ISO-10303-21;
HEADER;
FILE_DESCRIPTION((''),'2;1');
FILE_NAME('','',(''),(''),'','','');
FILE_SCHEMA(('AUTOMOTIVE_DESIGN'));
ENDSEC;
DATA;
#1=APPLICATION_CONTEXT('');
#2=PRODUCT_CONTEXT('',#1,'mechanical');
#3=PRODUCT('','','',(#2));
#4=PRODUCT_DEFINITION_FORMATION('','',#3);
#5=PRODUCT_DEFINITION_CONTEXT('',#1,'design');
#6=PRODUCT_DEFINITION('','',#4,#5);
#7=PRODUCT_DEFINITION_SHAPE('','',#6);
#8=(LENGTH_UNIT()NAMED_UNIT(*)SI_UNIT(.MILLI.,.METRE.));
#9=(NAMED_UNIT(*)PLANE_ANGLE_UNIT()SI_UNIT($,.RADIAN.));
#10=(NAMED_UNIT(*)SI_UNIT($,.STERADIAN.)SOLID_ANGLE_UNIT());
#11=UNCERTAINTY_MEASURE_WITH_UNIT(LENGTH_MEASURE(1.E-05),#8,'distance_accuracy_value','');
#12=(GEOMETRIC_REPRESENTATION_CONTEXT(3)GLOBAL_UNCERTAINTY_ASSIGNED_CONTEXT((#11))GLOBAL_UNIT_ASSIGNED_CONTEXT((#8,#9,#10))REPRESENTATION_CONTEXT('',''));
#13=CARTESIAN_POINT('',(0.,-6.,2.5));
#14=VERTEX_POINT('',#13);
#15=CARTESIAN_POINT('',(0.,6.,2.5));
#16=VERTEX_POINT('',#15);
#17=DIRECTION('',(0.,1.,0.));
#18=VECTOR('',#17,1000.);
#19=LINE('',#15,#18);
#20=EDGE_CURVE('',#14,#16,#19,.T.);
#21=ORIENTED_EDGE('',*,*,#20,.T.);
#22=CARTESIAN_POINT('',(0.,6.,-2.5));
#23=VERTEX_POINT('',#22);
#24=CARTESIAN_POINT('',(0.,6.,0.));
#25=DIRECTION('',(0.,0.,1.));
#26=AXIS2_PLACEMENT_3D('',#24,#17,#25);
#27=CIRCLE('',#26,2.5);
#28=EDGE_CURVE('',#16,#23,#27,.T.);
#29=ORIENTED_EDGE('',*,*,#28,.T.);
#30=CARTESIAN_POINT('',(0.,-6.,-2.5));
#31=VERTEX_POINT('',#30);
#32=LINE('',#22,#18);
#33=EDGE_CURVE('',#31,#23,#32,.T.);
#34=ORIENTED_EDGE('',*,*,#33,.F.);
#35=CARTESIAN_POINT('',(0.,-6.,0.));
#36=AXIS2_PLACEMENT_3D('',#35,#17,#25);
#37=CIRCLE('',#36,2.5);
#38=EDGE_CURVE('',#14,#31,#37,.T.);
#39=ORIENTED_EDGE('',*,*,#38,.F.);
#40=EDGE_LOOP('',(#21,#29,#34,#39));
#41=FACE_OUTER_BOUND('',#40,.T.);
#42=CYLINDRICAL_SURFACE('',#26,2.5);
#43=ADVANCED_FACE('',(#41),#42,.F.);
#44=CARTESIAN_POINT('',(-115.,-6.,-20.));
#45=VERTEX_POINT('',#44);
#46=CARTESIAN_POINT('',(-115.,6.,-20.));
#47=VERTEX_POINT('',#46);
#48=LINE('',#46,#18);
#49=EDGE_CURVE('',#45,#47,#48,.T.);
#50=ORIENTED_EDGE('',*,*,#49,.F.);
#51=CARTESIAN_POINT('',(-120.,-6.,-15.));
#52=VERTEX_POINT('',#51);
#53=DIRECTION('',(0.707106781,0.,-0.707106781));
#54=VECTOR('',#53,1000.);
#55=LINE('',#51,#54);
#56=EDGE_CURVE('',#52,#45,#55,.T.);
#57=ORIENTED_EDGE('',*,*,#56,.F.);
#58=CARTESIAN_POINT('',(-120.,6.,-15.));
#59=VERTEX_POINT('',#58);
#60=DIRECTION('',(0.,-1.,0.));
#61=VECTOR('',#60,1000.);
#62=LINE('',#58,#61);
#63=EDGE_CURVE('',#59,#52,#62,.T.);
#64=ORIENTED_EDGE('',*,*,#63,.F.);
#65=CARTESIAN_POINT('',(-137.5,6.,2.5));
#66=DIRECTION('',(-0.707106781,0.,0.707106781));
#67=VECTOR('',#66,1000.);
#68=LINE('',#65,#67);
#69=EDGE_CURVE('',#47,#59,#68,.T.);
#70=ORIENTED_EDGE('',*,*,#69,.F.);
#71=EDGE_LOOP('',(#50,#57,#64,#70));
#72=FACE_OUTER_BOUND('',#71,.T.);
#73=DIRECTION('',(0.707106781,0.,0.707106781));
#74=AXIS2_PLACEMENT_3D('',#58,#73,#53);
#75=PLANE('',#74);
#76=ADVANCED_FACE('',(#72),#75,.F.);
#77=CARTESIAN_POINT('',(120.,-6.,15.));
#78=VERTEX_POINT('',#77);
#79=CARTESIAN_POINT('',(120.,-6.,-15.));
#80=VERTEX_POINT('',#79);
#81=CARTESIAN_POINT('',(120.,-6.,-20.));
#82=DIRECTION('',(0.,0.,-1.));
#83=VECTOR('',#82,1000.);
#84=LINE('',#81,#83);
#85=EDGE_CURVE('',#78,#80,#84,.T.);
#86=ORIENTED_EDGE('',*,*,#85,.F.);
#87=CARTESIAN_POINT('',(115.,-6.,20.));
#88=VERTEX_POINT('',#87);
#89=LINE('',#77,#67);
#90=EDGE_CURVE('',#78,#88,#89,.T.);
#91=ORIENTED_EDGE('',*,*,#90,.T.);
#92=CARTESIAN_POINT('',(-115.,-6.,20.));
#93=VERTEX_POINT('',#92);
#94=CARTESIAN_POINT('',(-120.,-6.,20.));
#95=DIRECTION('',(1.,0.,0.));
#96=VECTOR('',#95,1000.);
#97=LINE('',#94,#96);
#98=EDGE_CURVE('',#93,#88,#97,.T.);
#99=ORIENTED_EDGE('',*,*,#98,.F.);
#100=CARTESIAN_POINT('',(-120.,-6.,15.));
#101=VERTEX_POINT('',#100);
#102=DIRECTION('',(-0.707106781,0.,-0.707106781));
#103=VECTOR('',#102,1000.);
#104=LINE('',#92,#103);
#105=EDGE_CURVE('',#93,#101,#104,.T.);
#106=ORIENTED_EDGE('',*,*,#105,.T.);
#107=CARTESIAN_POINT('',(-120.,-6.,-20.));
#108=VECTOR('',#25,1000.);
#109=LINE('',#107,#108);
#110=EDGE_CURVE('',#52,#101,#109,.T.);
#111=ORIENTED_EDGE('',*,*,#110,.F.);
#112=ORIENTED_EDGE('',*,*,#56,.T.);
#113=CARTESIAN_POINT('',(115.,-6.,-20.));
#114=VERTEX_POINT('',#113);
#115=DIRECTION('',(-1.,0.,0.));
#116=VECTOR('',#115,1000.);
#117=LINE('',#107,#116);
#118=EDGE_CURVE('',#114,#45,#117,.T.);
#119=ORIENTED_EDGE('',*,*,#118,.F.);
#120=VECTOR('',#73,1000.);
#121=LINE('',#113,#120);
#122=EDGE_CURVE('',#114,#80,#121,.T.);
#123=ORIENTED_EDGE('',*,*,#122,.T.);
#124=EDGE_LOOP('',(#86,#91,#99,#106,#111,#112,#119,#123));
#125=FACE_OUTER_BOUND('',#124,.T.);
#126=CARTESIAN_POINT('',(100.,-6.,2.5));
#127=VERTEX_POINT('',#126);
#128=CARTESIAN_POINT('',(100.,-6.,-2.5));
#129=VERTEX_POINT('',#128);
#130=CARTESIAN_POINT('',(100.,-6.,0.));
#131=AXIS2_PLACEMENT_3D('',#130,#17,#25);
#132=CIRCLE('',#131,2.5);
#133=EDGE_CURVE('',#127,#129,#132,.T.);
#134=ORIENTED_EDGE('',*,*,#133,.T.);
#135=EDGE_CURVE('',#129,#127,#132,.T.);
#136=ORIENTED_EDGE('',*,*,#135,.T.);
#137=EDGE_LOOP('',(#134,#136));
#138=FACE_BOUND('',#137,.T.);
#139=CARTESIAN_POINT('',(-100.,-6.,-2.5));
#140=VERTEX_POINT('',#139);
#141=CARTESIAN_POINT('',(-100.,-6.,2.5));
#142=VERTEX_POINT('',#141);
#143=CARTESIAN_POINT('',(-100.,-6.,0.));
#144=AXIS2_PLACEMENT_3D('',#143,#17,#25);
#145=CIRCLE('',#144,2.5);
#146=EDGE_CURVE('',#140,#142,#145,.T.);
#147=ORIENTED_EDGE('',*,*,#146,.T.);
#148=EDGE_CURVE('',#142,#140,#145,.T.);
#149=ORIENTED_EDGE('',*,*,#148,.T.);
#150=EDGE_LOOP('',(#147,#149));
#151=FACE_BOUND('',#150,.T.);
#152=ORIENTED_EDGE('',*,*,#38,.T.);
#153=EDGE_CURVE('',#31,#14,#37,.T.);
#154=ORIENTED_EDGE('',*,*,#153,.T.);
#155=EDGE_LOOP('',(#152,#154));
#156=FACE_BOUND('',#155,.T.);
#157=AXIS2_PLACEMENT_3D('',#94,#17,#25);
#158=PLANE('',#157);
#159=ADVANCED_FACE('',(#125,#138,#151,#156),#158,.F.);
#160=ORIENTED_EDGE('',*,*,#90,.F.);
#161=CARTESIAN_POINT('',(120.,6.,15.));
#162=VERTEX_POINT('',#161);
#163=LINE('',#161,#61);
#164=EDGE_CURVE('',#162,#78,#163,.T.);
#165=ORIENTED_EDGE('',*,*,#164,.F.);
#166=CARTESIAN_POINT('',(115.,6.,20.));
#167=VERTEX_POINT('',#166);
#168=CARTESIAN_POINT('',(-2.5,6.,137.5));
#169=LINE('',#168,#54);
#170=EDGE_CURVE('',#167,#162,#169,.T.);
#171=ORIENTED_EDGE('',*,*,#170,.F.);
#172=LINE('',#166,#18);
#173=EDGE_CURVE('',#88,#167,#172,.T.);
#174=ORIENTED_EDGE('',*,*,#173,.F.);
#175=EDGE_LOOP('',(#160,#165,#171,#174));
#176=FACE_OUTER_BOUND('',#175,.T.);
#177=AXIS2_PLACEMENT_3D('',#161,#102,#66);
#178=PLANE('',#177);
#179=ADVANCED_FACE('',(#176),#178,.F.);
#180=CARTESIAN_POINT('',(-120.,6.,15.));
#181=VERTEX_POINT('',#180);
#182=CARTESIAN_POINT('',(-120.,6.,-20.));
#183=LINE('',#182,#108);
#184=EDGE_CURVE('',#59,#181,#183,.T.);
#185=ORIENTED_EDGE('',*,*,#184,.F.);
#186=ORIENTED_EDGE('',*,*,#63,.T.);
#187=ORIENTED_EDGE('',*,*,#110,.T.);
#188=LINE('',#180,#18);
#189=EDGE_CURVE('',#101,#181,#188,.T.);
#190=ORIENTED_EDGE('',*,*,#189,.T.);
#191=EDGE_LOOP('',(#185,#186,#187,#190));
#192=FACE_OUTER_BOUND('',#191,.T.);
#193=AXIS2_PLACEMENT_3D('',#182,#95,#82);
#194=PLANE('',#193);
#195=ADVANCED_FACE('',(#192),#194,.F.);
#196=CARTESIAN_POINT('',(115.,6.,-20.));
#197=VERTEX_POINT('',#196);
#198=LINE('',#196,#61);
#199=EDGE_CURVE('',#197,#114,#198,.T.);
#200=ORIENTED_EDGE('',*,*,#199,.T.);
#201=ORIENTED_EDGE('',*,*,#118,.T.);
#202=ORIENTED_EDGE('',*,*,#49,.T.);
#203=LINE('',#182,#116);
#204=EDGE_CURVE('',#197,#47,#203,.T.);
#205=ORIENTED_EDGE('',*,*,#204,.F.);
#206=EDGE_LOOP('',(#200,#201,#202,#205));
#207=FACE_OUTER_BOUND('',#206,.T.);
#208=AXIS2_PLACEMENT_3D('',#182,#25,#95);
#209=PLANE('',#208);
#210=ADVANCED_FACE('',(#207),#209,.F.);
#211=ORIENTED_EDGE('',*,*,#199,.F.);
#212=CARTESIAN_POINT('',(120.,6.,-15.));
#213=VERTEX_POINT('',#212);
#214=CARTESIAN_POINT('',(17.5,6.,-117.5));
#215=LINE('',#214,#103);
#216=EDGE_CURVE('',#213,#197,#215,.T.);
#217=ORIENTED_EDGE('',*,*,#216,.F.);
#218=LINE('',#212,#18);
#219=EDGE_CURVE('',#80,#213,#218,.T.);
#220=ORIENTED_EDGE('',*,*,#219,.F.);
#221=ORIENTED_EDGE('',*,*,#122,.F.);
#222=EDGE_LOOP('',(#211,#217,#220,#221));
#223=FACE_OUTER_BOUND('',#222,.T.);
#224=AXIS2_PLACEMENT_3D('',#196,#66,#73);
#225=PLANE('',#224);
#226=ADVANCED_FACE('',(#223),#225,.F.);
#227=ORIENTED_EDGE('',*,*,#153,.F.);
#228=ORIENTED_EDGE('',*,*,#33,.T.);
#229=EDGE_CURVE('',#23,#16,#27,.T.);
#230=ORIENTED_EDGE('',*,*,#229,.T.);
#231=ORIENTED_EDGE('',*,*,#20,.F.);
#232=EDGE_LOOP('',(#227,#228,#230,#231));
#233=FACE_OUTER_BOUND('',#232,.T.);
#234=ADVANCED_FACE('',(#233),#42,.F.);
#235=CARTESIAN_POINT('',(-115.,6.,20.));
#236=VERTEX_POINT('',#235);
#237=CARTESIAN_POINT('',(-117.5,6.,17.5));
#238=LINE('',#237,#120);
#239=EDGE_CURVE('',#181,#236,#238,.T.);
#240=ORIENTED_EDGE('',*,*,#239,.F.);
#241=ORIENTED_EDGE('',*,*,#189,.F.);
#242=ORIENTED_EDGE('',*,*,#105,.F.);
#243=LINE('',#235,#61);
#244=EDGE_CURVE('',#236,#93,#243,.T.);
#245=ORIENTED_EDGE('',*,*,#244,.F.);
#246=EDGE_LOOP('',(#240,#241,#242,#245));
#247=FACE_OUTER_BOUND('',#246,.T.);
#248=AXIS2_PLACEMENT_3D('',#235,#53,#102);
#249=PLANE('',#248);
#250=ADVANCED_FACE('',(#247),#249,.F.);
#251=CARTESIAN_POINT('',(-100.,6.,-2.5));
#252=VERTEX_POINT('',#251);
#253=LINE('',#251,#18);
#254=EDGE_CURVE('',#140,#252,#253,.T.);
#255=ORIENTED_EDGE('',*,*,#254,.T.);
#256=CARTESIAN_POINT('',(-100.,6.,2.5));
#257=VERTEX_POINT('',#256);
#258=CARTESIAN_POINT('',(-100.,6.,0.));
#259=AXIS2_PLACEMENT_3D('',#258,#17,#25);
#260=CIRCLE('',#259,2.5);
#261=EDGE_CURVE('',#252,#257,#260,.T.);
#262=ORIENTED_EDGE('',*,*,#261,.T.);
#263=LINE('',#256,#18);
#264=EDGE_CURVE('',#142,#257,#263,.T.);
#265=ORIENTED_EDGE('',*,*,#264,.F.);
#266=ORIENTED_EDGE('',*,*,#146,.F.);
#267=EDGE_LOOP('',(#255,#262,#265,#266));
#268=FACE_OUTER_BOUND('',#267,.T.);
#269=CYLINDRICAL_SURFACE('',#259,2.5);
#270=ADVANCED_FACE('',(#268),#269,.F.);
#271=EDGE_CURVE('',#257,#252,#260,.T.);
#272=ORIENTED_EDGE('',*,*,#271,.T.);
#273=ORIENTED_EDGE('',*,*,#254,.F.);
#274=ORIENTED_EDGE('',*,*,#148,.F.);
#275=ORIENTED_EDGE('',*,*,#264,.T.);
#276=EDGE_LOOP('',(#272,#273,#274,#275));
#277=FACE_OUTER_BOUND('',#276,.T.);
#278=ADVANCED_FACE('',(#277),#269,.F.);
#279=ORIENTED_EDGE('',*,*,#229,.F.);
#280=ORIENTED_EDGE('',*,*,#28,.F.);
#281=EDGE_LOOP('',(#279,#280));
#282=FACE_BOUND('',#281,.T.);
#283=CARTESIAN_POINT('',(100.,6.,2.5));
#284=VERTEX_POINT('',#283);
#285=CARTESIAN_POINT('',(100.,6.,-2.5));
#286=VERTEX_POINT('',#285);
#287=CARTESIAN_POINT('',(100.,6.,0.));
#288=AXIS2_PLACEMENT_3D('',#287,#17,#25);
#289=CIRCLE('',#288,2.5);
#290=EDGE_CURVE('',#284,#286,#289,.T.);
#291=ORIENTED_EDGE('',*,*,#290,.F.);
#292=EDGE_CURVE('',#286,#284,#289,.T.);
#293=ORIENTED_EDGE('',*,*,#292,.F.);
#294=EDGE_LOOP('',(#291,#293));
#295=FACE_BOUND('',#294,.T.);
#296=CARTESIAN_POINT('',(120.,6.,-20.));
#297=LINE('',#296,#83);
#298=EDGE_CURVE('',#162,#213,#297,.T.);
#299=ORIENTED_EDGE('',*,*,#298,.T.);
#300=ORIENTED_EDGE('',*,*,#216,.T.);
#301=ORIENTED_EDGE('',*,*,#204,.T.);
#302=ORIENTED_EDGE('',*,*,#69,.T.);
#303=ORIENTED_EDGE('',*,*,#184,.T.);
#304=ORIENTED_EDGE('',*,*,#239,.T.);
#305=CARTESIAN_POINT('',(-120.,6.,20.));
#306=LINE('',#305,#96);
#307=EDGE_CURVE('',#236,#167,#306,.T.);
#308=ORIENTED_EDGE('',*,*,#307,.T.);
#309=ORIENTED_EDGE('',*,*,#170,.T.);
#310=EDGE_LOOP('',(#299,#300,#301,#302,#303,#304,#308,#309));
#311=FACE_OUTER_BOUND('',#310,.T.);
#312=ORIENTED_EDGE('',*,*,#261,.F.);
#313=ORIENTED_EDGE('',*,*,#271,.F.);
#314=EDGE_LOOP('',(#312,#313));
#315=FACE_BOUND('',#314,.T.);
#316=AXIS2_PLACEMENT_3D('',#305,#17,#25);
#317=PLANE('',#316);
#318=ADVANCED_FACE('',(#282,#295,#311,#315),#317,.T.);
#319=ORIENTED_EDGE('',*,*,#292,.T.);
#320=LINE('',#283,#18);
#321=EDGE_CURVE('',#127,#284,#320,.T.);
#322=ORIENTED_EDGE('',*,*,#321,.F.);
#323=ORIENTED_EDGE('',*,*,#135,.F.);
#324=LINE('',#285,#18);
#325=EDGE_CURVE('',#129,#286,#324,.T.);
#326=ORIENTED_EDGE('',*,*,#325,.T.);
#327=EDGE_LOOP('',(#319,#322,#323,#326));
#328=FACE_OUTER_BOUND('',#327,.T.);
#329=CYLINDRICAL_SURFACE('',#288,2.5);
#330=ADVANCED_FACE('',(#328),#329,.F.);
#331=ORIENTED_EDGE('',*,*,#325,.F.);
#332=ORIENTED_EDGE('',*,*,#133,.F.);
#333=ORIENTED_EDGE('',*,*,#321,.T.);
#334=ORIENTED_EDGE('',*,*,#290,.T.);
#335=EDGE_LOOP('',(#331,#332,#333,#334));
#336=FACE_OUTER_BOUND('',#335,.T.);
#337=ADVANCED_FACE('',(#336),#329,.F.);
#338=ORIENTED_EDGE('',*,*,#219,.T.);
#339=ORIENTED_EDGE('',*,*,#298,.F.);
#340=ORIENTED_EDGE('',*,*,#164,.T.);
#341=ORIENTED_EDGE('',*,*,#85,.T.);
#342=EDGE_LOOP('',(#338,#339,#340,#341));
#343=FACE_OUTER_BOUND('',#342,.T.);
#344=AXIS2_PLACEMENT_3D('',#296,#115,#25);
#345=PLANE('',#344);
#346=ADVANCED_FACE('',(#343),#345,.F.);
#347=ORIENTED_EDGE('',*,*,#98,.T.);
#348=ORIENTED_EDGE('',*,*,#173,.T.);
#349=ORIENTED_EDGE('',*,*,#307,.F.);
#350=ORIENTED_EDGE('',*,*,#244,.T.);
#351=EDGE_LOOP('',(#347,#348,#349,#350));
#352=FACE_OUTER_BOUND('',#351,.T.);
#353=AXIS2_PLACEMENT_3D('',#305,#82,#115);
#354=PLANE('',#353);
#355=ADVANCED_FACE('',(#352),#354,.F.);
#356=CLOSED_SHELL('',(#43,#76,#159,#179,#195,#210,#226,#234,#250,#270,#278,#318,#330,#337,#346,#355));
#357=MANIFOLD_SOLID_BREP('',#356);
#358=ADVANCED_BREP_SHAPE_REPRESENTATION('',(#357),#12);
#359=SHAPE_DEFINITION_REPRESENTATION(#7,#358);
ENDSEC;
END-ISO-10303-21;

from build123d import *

# Parameters (mm, degrees)
SKETCH1_W             = 240
SKETCH1_H             = 40
EXTRUDE1_DEPTH        = 6
M6_TAPPED_HOLE1_D     = 5
M6_TAPPED_HOLE1_DEPTH = 15
M6_TAPPED_HOLE1_TIP   = 1.502151548
CHAMFER1_SIZE         = 5


with BuildPart() as part:
    # Sketch1 → Extrude1 (new, symmetric)
    with BuildSketch(Plane(origin=(0, 0, 0), x_dir=(1, 0, 0), z_dir=(0, 1, 0))):
        Rectangle(SKETCH1_W, SKETCH1_H)
    extrude(amount=EXTRUDE1_DEPTH, both=True)

    # M6 Tapped Hole1
    with Locations(Plane(origin=(0, 6, 0), x_dir=(-1, 0, 0), z_dir=(0, 1, 0))):
        with Locations((100, 0), (0, 0), (-100, 0)):
            Hole(M6_TAPPED_HOLE1_D / 2, depth=M6_TAPPED_HOLE1_DEPTH)
            with Locations((0, 0, -(M6_TAPPED_HOLE1_DEPTH + M6_TAPPED_HOLE1_TIP / 2))):  # 118° drill point
                Cone(0, M6_TAPPED_HOLE1_D / 2, M6_TAPPED_HOLE1_TIP, mode=Mode.SUBTRACT)

    # Chamfer1
    chamfer1_edges = [part.edges().sort_by_distance(p)[0] for p in [
        (-120, 0, -20),
        (120, 0, -20),
        (120, 0, 20),
        (-120, 0, 20),
    ]]
    chamfer(chamfer1_edges, length=CHAMFER1_SIZE)


solid = part.part
